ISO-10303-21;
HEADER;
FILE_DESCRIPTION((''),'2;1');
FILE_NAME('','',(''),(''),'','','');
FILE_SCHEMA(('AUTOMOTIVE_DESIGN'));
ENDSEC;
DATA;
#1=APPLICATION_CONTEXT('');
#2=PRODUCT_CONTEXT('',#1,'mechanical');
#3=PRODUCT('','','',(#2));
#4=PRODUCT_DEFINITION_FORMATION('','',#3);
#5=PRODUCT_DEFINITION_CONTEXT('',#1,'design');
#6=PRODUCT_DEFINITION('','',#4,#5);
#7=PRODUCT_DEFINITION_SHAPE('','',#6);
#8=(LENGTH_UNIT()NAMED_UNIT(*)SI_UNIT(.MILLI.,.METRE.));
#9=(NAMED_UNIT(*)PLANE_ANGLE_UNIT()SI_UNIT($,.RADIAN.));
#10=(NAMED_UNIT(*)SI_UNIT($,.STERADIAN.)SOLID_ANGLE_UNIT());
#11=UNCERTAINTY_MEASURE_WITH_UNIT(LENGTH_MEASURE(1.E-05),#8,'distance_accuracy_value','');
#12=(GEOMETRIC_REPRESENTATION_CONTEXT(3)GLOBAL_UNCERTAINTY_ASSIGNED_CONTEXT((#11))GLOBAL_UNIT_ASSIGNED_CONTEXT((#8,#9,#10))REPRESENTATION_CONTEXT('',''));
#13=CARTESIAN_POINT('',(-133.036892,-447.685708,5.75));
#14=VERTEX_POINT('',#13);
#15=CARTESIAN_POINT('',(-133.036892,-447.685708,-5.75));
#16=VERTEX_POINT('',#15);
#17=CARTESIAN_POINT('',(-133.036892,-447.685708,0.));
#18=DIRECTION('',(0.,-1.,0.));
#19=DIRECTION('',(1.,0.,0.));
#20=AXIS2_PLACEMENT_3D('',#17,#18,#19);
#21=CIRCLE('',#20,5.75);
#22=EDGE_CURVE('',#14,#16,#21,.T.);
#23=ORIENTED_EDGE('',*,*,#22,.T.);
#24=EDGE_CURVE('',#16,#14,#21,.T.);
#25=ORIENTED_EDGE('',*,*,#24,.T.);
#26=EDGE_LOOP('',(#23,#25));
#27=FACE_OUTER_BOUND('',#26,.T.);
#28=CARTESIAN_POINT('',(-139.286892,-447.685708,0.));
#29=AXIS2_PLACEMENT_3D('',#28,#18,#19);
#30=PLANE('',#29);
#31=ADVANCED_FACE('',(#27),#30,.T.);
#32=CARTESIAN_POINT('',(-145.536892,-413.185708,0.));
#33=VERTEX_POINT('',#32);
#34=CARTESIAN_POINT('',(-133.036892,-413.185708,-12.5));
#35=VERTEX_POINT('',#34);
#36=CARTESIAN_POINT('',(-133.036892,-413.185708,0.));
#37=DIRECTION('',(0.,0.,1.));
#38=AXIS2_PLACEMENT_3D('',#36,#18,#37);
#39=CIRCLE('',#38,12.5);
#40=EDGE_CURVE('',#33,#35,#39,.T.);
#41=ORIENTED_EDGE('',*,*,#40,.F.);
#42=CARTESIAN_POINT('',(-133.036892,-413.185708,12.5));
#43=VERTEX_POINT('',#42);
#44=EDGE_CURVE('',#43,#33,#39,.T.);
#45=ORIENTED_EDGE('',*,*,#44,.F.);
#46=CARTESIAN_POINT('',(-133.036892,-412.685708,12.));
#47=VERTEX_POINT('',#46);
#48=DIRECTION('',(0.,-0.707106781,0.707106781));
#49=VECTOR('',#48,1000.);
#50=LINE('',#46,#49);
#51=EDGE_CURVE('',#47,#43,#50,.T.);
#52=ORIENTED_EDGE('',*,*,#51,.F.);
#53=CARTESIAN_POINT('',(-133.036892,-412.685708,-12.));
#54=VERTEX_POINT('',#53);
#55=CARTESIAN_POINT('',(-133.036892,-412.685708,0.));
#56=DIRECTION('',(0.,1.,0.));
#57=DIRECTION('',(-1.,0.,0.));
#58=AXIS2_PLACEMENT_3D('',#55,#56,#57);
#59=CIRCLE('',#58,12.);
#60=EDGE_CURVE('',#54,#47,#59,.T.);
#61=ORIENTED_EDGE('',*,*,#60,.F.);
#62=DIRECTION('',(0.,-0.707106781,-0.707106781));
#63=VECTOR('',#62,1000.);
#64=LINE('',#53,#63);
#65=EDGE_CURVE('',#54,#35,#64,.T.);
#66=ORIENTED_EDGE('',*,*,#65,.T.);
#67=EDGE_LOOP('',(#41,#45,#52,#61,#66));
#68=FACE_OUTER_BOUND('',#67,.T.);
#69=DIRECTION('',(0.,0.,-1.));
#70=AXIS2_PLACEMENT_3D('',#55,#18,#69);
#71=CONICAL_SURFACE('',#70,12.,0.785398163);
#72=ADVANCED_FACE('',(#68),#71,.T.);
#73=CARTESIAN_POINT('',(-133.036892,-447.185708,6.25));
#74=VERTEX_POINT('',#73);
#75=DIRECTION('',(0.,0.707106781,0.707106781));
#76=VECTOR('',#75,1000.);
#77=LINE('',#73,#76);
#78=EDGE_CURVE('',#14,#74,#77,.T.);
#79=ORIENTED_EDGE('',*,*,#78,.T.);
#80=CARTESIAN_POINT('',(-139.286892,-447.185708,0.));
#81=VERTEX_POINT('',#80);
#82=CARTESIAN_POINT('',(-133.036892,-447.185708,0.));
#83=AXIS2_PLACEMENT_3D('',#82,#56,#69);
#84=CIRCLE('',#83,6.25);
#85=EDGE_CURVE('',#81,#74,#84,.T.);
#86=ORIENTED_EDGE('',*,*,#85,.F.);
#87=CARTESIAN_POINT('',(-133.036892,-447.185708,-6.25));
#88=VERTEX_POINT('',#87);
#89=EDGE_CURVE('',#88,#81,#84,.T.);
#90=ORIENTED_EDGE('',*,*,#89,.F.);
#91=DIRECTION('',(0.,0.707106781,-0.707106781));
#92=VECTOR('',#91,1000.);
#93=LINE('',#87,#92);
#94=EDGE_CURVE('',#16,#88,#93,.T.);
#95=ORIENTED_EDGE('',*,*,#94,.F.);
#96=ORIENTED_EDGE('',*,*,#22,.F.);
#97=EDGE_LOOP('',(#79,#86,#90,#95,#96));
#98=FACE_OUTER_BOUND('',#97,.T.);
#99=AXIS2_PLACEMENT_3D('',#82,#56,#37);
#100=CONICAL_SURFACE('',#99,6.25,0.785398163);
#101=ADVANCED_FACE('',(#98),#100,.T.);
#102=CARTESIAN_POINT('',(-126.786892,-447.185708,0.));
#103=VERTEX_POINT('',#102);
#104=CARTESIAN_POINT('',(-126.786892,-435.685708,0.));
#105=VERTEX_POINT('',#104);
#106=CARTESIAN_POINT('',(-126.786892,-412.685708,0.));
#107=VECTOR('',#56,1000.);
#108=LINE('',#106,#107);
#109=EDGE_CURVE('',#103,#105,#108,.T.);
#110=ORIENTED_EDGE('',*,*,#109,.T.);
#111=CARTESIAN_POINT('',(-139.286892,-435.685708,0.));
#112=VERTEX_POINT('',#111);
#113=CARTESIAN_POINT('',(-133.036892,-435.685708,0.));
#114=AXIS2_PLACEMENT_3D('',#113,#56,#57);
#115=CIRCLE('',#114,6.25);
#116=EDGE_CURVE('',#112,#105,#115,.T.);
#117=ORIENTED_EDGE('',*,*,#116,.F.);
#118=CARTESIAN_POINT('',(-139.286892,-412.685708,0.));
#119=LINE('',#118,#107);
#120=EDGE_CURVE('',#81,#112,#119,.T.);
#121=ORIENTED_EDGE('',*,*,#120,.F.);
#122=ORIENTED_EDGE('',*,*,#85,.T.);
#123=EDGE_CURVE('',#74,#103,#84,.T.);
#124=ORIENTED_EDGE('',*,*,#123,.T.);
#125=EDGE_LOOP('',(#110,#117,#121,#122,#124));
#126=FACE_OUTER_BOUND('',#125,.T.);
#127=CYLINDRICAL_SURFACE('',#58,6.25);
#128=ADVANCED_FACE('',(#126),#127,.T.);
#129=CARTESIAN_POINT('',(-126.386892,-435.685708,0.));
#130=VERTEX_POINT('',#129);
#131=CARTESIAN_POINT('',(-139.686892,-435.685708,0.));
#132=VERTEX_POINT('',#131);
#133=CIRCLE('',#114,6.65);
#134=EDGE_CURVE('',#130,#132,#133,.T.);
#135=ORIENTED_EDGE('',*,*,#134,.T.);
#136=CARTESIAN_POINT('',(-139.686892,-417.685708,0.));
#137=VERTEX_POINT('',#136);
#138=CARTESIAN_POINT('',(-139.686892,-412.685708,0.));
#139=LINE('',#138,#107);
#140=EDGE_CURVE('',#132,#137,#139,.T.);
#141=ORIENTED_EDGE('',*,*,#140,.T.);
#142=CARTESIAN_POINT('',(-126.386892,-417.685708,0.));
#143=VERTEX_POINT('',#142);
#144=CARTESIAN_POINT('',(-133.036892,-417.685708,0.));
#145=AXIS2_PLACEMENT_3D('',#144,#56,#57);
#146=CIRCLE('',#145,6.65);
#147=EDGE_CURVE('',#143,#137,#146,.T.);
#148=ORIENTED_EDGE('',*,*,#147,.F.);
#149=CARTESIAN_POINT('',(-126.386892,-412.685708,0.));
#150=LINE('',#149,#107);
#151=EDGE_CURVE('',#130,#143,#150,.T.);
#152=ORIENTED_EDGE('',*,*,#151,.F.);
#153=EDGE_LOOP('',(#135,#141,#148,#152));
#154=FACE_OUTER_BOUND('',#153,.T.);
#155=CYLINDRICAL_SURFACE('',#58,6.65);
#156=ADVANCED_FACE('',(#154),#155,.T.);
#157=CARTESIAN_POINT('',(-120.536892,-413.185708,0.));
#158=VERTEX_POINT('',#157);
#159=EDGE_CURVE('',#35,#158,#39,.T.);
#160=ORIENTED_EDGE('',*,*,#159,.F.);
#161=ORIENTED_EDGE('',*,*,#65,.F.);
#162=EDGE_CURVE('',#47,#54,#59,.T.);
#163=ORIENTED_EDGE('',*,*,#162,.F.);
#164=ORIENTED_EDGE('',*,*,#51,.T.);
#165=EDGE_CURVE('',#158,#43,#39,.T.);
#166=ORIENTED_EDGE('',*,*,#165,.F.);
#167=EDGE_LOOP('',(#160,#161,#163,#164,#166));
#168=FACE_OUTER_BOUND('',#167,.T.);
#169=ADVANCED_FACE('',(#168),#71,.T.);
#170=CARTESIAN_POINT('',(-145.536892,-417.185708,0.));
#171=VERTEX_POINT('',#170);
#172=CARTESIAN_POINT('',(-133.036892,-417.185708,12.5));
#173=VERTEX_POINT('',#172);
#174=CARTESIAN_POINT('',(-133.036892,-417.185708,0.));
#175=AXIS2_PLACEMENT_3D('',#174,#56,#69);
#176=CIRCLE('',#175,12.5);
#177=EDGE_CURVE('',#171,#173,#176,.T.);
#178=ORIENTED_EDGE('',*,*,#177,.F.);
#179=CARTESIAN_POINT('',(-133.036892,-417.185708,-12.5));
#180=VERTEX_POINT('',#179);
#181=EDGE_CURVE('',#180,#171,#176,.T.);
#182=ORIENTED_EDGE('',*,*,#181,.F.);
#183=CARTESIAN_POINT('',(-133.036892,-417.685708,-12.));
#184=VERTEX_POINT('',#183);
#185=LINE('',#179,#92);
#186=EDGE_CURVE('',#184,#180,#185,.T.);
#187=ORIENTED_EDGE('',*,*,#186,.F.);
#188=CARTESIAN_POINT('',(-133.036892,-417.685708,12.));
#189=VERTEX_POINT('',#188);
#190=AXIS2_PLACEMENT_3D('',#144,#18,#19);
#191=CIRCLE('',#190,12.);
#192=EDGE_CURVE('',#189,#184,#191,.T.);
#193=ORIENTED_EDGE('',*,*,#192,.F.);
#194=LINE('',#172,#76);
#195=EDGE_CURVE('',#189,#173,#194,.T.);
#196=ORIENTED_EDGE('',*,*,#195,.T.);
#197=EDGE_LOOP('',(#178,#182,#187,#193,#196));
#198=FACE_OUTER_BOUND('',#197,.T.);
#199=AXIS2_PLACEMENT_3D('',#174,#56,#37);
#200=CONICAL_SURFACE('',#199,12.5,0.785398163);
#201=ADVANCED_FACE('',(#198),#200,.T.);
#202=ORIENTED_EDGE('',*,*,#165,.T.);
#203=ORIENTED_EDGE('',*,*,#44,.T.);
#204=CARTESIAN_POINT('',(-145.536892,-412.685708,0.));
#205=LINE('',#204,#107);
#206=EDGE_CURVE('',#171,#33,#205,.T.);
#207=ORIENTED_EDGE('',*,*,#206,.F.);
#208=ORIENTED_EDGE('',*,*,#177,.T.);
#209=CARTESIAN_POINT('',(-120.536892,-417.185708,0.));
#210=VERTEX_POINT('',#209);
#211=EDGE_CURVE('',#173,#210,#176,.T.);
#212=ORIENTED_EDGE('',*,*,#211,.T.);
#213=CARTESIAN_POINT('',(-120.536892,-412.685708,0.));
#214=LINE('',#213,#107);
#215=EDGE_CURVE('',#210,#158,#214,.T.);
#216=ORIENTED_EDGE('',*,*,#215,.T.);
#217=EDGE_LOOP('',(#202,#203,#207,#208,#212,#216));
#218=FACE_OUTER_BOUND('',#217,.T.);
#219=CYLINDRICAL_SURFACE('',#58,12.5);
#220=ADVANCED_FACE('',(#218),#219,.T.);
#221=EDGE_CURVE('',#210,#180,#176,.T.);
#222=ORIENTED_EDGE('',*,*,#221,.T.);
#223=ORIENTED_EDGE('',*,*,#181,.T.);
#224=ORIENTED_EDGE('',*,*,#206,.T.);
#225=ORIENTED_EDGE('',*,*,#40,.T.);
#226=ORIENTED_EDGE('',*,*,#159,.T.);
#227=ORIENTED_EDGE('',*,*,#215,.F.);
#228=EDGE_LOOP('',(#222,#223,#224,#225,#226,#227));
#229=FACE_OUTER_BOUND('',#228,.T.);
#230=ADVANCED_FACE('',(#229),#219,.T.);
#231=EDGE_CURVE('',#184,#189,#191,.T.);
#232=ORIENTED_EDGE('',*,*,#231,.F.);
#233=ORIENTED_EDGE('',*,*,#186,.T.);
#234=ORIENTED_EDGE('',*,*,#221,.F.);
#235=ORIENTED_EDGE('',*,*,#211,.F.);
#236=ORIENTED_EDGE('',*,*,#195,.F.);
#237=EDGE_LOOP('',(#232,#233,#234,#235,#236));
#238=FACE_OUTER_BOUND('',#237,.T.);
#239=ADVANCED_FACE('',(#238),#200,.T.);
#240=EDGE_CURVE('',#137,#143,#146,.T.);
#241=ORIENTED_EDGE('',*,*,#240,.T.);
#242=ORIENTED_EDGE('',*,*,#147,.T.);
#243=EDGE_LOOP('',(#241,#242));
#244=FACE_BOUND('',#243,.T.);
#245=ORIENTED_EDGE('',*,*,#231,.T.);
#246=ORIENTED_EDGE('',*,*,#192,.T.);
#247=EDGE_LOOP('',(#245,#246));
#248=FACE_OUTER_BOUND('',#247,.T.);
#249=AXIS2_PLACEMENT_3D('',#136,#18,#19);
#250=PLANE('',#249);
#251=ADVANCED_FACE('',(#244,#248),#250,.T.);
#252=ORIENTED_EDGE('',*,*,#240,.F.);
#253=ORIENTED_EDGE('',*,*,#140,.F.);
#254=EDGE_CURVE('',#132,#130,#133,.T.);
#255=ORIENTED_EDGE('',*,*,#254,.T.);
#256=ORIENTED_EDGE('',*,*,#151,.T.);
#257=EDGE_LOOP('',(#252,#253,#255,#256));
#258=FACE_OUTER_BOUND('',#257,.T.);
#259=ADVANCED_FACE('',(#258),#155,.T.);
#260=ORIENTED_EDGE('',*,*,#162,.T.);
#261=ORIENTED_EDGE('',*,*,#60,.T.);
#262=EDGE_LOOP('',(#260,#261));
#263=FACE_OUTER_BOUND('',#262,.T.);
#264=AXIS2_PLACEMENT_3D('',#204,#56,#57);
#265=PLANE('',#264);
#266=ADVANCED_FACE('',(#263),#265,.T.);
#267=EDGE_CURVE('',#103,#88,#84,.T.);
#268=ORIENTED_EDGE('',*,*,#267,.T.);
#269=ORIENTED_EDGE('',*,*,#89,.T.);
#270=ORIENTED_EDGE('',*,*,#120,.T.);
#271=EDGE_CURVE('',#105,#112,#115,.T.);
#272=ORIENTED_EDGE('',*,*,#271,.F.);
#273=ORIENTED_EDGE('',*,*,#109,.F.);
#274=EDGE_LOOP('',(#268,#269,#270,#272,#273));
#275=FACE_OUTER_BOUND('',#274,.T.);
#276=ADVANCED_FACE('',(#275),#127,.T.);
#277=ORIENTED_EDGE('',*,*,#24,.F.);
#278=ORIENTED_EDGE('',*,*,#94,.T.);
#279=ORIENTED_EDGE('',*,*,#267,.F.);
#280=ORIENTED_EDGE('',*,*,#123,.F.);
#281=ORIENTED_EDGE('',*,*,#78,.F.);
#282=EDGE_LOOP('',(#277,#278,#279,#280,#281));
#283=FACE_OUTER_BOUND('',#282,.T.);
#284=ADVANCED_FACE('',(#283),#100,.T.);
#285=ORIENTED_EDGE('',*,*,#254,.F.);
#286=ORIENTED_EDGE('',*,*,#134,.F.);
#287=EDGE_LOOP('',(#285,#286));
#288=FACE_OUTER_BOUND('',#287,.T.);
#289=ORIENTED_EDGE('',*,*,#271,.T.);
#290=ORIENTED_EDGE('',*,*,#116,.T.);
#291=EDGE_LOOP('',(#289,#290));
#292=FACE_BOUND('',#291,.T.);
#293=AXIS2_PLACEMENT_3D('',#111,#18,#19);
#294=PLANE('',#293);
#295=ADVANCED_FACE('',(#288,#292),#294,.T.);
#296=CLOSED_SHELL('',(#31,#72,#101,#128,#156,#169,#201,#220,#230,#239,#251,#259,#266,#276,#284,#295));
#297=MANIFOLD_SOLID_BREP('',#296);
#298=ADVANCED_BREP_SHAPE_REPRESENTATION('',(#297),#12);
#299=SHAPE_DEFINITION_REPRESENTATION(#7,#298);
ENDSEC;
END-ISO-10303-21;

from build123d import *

# Parameters (mm, degrees)
CHAMFER1_SIZE = 0.5


with BuildPart() as part:
    # Sketch1 → Revolve1 (revolve)
    with BuildSketch(Plane.XY):
        Polygon((-139.286891893, -435.685707644), (-139.686891893, -435.685707644), (-139.686891893, -417.685707644), (-145.536891893, -417.685707644), (-145.536891893, -412.685707644), (-133.036891893, -412.685707644), (-133.036891893, -447.685707644), (-139.286891893, -447.685707644), align=None)
    revolve(axis=Axis((-133.036891893, -412.685707644, 0), (0, -1, 0)))

    # Chamfer1
    chamfer1_edges = [part.edges().sort_by_distance(p)[0] for p in [
        (-120.536891893, -412.685707644, 0),
        (-120.536891893, -417.685707644, 0),
        (-126.786891893, -447.685707644, 0),
    ]]
    chamfer(chamfer1_edges, length=CHAMFER1_SIZE)


solid = part.part
